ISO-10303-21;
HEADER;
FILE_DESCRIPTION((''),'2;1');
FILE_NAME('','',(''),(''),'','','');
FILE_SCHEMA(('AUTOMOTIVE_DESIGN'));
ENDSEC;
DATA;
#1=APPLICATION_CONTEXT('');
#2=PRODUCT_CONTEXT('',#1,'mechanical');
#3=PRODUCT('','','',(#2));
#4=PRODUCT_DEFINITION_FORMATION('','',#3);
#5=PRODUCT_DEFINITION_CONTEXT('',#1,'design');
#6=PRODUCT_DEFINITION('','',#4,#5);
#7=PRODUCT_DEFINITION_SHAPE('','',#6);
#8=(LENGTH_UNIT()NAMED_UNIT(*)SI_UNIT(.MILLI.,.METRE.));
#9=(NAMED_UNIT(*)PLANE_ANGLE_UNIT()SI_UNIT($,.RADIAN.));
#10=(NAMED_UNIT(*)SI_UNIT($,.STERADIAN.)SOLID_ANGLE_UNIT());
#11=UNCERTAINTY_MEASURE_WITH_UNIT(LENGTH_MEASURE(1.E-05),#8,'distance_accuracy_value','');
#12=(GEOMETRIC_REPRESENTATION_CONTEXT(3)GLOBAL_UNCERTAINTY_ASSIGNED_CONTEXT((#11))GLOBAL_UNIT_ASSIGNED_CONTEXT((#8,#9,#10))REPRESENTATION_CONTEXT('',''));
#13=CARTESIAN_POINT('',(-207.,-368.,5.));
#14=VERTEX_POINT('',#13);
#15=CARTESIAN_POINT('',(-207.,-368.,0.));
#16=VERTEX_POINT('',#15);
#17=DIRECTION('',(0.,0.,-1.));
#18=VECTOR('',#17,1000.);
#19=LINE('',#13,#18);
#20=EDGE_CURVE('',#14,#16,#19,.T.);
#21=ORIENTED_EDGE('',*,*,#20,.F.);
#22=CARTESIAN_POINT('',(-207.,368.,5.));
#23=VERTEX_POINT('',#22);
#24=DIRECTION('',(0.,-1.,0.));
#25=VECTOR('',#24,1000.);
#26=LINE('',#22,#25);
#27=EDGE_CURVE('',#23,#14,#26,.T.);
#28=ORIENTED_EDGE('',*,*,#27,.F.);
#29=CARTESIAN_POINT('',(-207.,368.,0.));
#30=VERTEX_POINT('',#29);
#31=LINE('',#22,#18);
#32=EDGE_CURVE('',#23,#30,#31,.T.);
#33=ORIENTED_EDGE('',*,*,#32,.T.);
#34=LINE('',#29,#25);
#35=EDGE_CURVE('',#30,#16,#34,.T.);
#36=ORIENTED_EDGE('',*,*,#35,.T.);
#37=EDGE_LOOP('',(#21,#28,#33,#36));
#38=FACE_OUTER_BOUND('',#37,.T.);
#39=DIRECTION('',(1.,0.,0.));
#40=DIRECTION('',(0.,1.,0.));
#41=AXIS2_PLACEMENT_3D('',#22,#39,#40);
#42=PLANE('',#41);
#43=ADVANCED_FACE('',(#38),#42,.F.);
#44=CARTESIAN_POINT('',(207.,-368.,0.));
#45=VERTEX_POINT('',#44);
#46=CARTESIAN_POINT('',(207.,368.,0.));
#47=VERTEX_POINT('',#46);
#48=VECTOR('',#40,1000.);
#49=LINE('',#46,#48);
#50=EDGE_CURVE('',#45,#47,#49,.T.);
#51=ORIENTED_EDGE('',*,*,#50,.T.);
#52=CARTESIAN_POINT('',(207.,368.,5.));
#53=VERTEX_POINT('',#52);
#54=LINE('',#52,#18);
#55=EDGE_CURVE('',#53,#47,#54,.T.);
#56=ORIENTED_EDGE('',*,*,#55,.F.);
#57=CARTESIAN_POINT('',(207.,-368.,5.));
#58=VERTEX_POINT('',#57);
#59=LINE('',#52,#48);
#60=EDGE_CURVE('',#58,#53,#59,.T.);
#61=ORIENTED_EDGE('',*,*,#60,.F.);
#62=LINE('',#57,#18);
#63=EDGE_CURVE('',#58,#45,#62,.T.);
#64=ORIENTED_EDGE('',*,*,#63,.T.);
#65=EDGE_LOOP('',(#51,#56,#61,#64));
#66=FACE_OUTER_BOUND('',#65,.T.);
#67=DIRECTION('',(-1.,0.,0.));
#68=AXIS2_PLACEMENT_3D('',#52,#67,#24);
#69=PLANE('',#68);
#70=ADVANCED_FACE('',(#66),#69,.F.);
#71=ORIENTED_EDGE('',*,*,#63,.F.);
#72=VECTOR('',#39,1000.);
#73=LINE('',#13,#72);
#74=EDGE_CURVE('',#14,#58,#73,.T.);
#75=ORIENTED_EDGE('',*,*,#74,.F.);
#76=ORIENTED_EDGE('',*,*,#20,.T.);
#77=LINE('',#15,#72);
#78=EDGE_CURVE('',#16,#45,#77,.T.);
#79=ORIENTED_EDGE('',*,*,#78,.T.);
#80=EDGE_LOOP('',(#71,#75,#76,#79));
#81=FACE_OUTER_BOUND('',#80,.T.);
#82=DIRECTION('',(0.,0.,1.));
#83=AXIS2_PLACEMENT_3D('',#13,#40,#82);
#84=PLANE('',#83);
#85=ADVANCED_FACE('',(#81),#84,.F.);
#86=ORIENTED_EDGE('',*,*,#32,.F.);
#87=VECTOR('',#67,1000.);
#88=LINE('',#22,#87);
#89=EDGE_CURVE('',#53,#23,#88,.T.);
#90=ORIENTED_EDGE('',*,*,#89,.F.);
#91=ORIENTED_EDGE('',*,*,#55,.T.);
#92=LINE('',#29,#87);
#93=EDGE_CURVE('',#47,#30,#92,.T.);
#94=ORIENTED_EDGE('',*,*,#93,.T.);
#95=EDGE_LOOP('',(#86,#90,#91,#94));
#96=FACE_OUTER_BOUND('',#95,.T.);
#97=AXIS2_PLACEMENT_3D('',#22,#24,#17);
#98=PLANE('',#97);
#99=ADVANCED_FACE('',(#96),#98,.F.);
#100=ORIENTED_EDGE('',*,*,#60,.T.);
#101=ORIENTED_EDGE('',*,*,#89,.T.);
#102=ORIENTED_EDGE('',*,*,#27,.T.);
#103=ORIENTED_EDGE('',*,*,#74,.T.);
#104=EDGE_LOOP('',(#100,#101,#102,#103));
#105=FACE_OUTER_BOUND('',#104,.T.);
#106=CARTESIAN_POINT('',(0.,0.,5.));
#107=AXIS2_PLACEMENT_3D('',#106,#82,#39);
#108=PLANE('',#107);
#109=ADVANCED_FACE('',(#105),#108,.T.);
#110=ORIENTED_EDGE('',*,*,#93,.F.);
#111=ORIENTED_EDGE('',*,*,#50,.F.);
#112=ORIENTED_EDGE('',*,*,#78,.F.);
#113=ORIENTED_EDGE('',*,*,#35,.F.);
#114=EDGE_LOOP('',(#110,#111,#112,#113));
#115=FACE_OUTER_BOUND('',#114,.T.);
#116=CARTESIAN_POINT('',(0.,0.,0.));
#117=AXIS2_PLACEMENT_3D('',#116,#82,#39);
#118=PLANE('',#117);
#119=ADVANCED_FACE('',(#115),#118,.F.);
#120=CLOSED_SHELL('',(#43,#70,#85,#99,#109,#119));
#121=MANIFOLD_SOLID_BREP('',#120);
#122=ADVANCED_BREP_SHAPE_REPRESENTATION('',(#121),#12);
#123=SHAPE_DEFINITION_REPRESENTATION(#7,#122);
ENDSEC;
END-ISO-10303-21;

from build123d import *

# Parameters (mm, degrees)
SKETCH_1_W      = 414
SKETCH_1_H      = 736
EXTRUDE_1_DEPTH = 5


with BuildPart() as part:
    # 草图1 → 凸台-拉伸1 (new body)
    with BuildSketch(Plane.XY):
        Rectangle(SKETCH_1_W, SKETCH_1_H)
    extrude(amount=EXTRUDE_1_DEPTH)


solid = part.part
